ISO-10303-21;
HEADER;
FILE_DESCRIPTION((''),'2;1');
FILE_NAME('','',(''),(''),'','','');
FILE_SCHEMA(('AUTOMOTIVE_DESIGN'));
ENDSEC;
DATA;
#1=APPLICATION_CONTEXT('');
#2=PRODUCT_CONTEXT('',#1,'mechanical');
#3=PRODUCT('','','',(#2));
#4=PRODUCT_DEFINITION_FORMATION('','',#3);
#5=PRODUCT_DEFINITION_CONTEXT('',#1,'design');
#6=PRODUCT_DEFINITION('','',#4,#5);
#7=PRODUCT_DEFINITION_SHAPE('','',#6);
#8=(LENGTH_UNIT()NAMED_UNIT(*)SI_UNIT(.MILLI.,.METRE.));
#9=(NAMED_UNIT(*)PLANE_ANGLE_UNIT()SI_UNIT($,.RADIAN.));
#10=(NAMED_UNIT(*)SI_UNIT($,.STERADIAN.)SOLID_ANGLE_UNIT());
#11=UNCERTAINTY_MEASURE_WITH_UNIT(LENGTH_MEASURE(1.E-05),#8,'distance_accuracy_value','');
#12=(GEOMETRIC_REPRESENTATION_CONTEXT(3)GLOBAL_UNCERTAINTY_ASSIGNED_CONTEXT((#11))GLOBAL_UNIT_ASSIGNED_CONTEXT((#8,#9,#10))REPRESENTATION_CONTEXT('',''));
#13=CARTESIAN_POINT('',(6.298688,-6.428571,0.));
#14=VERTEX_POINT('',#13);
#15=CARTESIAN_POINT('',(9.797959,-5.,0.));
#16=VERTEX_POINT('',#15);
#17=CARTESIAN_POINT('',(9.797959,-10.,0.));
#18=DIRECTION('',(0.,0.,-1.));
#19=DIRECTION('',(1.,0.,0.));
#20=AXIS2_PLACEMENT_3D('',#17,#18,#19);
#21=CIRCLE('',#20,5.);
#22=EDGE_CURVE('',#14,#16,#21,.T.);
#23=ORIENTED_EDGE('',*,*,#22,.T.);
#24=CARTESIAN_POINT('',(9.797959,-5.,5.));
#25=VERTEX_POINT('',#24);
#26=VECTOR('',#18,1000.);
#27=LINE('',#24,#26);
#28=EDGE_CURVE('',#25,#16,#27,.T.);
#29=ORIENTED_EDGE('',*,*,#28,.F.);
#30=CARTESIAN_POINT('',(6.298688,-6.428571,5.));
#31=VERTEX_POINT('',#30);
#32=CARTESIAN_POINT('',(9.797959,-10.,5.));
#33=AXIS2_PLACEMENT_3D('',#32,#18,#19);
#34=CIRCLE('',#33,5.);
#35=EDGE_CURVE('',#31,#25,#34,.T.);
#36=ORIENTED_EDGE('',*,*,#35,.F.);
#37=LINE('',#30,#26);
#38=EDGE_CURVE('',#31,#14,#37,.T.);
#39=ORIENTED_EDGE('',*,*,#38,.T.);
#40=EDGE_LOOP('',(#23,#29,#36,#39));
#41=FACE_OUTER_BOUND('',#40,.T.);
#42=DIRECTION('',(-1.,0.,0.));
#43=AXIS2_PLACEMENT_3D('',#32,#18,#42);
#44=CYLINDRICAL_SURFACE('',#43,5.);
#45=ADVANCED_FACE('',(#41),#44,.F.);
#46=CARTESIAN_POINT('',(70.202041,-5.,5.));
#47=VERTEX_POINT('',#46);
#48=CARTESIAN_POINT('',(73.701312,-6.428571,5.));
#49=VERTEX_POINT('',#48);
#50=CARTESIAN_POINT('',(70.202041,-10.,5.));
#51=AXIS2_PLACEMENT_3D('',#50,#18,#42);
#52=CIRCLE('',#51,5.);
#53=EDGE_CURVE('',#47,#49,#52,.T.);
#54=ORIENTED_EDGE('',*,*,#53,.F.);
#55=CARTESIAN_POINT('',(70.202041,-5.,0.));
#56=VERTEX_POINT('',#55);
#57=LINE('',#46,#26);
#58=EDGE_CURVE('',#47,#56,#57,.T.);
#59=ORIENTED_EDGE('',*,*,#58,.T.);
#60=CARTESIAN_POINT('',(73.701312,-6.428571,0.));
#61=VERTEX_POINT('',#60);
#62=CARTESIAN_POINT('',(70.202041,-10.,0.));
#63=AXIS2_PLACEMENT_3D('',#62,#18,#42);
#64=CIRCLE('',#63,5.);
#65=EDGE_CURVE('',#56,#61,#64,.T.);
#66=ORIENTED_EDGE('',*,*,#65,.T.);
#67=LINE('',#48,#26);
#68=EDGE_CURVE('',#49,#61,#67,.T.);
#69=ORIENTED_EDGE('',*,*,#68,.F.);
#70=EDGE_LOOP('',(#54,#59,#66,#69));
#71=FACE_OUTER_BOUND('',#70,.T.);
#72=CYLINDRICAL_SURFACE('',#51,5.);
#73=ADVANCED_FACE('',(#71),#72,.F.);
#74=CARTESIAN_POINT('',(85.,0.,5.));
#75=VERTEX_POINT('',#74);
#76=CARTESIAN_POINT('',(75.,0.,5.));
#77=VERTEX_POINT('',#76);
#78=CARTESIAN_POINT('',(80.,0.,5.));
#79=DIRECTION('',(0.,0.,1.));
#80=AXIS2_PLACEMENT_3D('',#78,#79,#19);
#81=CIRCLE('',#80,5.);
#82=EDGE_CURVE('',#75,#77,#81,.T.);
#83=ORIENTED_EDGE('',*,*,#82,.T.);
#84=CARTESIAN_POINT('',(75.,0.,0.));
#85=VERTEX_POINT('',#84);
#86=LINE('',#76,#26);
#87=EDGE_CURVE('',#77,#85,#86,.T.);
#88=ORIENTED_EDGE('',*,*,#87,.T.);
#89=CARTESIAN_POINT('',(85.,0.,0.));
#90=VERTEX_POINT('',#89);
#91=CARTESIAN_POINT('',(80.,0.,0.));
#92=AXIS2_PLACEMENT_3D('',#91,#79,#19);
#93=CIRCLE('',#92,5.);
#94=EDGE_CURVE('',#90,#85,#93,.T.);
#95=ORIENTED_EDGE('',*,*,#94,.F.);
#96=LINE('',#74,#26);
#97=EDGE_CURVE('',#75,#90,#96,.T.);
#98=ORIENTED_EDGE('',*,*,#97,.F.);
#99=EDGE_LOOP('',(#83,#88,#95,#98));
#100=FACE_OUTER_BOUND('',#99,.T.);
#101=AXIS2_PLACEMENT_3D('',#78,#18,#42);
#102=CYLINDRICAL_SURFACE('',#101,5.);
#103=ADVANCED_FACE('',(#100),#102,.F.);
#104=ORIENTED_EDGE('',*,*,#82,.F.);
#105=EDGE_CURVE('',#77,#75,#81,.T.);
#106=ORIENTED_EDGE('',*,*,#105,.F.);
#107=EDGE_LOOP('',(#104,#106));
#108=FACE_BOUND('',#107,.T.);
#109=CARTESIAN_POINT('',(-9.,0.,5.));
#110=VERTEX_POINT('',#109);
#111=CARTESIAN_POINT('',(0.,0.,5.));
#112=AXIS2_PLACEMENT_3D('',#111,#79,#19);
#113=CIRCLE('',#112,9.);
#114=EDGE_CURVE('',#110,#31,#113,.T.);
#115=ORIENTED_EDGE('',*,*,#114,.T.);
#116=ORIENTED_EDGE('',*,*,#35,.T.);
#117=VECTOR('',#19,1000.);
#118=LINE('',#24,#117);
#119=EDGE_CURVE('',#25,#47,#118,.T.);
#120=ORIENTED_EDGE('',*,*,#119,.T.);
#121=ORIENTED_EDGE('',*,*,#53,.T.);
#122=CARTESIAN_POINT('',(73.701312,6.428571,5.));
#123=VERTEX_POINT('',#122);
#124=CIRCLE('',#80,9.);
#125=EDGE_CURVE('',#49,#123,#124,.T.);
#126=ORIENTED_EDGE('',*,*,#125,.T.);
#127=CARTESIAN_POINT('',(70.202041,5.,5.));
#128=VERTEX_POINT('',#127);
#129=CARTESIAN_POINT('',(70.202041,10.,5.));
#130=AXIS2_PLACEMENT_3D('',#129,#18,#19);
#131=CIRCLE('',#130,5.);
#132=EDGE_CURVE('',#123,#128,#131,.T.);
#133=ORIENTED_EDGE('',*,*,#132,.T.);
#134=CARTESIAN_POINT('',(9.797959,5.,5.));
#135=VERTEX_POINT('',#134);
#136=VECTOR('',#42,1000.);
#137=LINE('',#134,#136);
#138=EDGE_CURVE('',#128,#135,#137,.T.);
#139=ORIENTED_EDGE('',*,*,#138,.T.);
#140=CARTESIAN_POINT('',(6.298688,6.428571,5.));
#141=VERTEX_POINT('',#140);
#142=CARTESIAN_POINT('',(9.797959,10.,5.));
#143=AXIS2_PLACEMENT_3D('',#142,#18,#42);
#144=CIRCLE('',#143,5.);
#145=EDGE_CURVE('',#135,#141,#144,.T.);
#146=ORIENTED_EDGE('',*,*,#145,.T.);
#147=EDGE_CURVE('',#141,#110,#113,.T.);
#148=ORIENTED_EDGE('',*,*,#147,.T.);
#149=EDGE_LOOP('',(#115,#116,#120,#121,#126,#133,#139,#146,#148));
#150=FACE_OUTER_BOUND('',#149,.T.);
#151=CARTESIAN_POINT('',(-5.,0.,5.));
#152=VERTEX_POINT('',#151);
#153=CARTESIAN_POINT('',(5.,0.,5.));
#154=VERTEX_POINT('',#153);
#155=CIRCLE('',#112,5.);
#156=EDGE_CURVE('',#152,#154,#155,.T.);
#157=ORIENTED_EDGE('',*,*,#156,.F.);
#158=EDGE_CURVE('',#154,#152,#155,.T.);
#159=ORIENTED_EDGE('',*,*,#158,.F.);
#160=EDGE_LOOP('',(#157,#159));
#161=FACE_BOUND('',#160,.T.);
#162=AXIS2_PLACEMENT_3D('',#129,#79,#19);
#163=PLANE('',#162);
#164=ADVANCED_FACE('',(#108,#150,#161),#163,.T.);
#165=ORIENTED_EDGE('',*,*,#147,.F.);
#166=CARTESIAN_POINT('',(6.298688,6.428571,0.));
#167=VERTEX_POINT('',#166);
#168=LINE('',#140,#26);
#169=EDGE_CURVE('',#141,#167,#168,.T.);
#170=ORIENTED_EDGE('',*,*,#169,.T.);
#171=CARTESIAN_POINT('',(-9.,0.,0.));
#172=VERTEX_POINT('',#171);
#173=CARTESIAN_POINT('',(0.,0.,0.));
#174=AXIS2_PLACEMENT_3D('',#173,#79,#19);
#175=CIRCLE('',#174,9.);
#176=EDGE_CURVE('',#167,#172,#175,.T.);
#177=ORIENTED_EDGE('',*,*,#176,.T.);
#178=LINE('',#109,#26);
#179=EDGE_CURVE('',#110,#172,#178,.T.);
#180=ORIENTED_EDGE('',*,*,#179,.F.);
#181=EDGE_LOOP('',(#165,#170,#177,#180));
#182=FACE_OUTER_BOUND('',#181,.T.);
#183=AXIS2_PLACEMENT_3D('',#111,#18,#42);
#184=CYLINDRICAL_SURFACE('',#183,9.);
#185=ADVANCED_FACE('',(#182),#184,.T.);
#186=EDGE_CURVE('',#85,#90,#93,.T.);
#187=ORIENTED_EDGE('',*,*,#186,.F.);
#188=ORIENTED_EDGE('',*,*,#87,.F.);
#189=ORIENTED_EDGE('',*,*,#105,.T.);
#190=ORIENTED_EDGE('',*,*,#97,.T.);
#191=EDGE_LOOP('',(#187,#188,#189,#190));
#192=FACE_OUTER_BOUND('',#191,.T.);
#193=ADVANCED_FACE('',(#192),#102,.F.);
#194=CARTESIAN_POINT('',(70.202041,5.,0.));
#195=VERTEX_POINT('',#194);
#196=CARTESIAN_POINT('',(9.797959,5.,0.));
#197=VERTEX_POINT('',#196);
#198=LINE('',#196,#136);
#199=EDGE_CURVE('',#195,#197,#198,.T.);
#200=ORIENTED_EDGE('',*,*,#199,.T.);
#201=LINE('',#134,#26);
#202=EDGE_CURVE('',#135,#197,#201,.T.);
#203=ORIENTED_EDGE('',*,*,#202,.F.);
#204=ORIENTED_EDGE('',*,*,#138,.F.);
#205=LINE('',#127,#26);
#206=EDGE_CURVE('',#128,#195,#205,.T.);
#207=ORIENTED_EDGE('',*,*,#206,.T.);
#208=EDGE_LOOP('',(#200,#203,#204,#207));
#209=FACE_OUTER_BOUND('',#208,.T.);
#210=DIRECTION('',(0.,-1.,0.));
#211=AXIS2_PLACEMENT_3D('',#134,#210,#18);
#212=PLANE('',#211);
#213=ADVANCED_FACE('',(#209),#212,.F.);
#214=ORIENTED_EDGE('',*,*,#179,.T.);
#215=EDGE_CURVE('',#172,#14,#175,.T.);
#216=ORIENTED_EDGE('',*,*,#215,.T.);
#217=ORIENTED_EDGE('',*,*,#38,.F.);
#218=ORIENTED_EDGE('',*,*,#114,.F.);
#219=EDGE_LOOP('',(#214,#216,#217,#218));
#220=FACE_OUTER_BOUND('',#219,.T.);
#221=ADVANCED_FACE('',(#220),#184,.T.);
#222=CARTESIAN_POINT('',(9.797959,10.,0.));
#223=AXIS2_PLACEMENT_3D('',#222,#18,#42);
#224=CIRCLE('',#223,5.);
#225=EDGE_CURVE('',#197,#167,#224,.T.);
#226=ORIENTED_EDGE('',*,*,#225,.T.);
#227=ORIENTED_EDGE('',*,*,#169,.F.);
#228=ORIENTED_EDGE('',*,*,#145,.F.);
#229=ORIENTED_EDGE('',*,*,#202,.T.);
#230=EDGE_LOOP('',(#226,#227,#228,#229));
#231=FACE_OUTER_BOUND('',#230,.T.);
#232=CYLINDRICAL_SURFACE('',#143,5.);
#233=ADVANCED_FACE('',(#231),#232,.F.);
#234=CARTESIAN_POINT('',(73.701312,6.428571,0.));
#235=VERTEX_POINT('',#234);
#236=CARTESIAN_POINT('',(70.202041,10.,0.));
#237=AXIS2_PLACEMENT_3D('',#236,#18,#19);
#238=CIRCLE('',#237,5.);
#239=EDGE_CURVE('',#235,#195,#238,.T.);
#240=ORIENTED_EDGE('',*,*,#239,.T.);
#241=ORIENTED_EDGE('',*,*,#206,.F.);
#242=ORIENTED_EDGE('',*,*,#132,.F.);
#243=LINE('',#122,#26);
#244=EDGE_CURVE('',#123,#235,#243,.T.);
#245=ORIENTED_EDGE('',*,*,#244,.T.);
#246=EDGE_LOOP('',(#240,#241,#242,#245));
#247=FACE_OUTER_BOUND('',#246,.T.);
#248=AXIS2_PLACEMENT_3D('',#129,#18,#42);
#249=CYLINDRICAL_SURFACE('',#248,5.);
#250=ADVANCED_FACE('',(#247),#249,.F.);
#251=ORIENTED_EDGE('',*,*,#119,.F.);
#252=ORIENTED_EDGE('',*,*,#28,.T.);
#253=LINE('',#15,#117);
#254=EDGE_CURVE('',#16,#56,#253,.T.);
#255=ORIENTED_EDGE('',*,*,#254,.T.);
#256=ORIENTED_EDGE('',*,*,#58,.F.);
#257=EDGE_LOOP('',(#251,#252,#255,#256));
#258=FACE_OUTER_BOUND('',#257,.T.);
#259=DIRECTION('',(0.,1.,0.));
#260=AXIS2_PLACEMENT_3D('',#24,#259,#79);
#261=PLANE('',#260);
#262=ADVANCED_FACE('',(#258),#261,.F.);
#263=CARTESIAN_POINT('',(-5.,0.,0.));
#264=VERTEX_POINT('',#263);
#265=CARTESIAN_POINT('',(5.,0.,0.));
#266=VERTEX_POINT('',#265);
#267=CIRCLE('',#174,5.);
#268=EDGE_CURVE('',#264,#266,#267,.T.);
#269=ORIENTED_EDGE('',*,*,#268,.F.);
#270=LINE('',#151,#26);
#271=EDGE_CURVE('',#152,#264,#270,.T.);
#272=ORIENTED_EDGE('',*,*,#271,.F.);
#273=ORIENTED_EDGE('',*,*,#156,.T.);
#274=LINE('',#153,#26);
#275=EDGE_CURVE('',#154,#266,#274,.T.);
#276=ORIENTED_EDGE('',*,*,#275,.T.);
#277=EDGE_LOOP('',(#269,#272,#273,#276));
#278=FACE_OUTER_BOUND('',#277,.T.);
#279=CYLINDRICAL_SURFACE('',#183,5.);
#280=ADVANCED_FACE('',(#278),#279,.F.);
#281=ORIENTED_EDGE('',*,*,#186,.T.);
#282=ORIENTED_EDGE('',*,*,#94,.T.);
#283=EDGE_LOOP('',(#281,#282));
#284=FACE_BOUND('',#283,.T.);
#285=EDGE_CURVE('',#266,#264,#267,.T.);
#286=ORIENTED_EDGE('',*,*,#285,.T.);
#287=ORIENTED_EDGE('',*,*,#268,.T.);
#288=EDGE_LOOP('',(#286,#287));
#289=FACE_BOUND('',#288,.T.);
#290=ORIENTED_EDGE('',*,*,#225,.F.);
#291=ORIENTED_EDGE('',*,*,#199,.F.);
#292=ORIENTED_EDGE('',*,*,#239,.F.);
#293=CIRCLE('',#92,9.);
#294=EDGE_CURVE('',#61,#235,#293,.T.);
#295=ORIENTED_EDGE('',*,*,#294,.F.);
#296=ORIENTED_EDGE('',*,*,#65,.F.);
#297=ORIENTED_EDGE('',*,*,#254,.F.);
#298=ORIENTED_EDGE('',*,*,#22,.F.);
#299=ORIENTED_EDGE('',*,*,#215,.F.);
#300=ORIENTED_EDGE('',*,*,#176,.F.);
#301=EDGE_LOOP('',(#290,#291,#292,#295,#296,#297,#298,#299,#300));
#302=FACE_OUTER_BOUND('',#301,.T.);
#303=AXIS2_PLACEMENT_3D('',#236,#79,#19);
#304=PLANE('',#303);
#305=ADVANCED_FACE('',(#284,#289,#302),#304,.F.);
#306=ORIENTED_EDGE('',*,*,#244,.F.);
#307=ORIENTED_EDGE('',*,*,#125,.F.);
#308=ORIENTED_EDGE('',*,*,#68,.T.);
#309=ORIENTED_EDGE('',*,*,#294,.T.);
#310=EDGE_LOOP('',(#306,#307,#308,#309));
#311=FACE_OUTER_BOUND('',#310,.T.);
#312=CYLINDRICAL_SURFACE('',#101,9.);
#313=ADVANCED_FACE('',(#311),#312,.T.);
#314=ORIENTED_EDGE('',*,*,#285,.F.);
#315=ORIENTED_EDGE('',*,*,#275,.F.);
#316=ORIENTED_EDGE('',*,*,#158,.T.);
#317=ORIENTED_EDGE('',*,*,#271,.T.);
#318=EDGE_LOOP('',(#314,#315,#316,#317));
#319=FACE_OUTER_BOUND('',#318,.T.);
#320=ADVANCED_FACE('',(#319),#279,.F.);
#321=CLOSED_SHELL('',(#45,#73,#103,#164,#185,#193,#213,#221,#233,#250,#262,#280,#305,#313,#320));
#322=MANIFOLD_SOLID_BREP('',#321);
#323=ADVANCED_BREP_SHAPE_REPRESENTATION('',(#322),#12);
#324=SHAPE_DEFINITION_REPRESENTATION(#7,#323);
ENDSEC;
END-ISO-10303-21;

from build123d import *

# Parameters (mm, degrees)
SKETCH1_R           = 5
BOSS_EXTRUDE1_DEPTH = 5


with BuildPart() as part:
    # Sketch1 → Boss-Extrude1 (new body)
    with BuildSketch(Plane.XY):
        with BuildLine():
            Line((9.797958971, 5), (70.202041029, 5))
            ThreePointArc((70.202041029, 5), (72.091863394, 5.370899501), (73.70131209, 6.428571429))
            ThreePointArc((73.70131209, 6.428571429), (89, 0), (73.70131209, -6.428571429))
            ThreePointArc((73.70131209, -6.428571429), (72.091863394, -5.370899501), (70.202041029, -5))
            Line((70.202041029, -5), (9.797958971, -5))
            ThreePointArc((9.797958971, -5), (7.908136606, -5.370899501), (6.29868791, -6.428571429))
            ThreePointArc((6.29868791, -6.428571429), (-9, 0), (6.29868791, 6.428571429))
            ThreePointArc((6.29868791, 6.428571429), (7.908136606, 5.370899501), (9.797958971, 5))
        make_face()
        Circle(SKETCH1_R, mode=Mode.SUBTRACT)
        with Locations((80, 0)):
            Circle(SKETCH1_R, mode=Mode.SUBTRACT)
    extrude(amount=BOSS_EXTRUDE1_DEPTH)


solid = part.part
